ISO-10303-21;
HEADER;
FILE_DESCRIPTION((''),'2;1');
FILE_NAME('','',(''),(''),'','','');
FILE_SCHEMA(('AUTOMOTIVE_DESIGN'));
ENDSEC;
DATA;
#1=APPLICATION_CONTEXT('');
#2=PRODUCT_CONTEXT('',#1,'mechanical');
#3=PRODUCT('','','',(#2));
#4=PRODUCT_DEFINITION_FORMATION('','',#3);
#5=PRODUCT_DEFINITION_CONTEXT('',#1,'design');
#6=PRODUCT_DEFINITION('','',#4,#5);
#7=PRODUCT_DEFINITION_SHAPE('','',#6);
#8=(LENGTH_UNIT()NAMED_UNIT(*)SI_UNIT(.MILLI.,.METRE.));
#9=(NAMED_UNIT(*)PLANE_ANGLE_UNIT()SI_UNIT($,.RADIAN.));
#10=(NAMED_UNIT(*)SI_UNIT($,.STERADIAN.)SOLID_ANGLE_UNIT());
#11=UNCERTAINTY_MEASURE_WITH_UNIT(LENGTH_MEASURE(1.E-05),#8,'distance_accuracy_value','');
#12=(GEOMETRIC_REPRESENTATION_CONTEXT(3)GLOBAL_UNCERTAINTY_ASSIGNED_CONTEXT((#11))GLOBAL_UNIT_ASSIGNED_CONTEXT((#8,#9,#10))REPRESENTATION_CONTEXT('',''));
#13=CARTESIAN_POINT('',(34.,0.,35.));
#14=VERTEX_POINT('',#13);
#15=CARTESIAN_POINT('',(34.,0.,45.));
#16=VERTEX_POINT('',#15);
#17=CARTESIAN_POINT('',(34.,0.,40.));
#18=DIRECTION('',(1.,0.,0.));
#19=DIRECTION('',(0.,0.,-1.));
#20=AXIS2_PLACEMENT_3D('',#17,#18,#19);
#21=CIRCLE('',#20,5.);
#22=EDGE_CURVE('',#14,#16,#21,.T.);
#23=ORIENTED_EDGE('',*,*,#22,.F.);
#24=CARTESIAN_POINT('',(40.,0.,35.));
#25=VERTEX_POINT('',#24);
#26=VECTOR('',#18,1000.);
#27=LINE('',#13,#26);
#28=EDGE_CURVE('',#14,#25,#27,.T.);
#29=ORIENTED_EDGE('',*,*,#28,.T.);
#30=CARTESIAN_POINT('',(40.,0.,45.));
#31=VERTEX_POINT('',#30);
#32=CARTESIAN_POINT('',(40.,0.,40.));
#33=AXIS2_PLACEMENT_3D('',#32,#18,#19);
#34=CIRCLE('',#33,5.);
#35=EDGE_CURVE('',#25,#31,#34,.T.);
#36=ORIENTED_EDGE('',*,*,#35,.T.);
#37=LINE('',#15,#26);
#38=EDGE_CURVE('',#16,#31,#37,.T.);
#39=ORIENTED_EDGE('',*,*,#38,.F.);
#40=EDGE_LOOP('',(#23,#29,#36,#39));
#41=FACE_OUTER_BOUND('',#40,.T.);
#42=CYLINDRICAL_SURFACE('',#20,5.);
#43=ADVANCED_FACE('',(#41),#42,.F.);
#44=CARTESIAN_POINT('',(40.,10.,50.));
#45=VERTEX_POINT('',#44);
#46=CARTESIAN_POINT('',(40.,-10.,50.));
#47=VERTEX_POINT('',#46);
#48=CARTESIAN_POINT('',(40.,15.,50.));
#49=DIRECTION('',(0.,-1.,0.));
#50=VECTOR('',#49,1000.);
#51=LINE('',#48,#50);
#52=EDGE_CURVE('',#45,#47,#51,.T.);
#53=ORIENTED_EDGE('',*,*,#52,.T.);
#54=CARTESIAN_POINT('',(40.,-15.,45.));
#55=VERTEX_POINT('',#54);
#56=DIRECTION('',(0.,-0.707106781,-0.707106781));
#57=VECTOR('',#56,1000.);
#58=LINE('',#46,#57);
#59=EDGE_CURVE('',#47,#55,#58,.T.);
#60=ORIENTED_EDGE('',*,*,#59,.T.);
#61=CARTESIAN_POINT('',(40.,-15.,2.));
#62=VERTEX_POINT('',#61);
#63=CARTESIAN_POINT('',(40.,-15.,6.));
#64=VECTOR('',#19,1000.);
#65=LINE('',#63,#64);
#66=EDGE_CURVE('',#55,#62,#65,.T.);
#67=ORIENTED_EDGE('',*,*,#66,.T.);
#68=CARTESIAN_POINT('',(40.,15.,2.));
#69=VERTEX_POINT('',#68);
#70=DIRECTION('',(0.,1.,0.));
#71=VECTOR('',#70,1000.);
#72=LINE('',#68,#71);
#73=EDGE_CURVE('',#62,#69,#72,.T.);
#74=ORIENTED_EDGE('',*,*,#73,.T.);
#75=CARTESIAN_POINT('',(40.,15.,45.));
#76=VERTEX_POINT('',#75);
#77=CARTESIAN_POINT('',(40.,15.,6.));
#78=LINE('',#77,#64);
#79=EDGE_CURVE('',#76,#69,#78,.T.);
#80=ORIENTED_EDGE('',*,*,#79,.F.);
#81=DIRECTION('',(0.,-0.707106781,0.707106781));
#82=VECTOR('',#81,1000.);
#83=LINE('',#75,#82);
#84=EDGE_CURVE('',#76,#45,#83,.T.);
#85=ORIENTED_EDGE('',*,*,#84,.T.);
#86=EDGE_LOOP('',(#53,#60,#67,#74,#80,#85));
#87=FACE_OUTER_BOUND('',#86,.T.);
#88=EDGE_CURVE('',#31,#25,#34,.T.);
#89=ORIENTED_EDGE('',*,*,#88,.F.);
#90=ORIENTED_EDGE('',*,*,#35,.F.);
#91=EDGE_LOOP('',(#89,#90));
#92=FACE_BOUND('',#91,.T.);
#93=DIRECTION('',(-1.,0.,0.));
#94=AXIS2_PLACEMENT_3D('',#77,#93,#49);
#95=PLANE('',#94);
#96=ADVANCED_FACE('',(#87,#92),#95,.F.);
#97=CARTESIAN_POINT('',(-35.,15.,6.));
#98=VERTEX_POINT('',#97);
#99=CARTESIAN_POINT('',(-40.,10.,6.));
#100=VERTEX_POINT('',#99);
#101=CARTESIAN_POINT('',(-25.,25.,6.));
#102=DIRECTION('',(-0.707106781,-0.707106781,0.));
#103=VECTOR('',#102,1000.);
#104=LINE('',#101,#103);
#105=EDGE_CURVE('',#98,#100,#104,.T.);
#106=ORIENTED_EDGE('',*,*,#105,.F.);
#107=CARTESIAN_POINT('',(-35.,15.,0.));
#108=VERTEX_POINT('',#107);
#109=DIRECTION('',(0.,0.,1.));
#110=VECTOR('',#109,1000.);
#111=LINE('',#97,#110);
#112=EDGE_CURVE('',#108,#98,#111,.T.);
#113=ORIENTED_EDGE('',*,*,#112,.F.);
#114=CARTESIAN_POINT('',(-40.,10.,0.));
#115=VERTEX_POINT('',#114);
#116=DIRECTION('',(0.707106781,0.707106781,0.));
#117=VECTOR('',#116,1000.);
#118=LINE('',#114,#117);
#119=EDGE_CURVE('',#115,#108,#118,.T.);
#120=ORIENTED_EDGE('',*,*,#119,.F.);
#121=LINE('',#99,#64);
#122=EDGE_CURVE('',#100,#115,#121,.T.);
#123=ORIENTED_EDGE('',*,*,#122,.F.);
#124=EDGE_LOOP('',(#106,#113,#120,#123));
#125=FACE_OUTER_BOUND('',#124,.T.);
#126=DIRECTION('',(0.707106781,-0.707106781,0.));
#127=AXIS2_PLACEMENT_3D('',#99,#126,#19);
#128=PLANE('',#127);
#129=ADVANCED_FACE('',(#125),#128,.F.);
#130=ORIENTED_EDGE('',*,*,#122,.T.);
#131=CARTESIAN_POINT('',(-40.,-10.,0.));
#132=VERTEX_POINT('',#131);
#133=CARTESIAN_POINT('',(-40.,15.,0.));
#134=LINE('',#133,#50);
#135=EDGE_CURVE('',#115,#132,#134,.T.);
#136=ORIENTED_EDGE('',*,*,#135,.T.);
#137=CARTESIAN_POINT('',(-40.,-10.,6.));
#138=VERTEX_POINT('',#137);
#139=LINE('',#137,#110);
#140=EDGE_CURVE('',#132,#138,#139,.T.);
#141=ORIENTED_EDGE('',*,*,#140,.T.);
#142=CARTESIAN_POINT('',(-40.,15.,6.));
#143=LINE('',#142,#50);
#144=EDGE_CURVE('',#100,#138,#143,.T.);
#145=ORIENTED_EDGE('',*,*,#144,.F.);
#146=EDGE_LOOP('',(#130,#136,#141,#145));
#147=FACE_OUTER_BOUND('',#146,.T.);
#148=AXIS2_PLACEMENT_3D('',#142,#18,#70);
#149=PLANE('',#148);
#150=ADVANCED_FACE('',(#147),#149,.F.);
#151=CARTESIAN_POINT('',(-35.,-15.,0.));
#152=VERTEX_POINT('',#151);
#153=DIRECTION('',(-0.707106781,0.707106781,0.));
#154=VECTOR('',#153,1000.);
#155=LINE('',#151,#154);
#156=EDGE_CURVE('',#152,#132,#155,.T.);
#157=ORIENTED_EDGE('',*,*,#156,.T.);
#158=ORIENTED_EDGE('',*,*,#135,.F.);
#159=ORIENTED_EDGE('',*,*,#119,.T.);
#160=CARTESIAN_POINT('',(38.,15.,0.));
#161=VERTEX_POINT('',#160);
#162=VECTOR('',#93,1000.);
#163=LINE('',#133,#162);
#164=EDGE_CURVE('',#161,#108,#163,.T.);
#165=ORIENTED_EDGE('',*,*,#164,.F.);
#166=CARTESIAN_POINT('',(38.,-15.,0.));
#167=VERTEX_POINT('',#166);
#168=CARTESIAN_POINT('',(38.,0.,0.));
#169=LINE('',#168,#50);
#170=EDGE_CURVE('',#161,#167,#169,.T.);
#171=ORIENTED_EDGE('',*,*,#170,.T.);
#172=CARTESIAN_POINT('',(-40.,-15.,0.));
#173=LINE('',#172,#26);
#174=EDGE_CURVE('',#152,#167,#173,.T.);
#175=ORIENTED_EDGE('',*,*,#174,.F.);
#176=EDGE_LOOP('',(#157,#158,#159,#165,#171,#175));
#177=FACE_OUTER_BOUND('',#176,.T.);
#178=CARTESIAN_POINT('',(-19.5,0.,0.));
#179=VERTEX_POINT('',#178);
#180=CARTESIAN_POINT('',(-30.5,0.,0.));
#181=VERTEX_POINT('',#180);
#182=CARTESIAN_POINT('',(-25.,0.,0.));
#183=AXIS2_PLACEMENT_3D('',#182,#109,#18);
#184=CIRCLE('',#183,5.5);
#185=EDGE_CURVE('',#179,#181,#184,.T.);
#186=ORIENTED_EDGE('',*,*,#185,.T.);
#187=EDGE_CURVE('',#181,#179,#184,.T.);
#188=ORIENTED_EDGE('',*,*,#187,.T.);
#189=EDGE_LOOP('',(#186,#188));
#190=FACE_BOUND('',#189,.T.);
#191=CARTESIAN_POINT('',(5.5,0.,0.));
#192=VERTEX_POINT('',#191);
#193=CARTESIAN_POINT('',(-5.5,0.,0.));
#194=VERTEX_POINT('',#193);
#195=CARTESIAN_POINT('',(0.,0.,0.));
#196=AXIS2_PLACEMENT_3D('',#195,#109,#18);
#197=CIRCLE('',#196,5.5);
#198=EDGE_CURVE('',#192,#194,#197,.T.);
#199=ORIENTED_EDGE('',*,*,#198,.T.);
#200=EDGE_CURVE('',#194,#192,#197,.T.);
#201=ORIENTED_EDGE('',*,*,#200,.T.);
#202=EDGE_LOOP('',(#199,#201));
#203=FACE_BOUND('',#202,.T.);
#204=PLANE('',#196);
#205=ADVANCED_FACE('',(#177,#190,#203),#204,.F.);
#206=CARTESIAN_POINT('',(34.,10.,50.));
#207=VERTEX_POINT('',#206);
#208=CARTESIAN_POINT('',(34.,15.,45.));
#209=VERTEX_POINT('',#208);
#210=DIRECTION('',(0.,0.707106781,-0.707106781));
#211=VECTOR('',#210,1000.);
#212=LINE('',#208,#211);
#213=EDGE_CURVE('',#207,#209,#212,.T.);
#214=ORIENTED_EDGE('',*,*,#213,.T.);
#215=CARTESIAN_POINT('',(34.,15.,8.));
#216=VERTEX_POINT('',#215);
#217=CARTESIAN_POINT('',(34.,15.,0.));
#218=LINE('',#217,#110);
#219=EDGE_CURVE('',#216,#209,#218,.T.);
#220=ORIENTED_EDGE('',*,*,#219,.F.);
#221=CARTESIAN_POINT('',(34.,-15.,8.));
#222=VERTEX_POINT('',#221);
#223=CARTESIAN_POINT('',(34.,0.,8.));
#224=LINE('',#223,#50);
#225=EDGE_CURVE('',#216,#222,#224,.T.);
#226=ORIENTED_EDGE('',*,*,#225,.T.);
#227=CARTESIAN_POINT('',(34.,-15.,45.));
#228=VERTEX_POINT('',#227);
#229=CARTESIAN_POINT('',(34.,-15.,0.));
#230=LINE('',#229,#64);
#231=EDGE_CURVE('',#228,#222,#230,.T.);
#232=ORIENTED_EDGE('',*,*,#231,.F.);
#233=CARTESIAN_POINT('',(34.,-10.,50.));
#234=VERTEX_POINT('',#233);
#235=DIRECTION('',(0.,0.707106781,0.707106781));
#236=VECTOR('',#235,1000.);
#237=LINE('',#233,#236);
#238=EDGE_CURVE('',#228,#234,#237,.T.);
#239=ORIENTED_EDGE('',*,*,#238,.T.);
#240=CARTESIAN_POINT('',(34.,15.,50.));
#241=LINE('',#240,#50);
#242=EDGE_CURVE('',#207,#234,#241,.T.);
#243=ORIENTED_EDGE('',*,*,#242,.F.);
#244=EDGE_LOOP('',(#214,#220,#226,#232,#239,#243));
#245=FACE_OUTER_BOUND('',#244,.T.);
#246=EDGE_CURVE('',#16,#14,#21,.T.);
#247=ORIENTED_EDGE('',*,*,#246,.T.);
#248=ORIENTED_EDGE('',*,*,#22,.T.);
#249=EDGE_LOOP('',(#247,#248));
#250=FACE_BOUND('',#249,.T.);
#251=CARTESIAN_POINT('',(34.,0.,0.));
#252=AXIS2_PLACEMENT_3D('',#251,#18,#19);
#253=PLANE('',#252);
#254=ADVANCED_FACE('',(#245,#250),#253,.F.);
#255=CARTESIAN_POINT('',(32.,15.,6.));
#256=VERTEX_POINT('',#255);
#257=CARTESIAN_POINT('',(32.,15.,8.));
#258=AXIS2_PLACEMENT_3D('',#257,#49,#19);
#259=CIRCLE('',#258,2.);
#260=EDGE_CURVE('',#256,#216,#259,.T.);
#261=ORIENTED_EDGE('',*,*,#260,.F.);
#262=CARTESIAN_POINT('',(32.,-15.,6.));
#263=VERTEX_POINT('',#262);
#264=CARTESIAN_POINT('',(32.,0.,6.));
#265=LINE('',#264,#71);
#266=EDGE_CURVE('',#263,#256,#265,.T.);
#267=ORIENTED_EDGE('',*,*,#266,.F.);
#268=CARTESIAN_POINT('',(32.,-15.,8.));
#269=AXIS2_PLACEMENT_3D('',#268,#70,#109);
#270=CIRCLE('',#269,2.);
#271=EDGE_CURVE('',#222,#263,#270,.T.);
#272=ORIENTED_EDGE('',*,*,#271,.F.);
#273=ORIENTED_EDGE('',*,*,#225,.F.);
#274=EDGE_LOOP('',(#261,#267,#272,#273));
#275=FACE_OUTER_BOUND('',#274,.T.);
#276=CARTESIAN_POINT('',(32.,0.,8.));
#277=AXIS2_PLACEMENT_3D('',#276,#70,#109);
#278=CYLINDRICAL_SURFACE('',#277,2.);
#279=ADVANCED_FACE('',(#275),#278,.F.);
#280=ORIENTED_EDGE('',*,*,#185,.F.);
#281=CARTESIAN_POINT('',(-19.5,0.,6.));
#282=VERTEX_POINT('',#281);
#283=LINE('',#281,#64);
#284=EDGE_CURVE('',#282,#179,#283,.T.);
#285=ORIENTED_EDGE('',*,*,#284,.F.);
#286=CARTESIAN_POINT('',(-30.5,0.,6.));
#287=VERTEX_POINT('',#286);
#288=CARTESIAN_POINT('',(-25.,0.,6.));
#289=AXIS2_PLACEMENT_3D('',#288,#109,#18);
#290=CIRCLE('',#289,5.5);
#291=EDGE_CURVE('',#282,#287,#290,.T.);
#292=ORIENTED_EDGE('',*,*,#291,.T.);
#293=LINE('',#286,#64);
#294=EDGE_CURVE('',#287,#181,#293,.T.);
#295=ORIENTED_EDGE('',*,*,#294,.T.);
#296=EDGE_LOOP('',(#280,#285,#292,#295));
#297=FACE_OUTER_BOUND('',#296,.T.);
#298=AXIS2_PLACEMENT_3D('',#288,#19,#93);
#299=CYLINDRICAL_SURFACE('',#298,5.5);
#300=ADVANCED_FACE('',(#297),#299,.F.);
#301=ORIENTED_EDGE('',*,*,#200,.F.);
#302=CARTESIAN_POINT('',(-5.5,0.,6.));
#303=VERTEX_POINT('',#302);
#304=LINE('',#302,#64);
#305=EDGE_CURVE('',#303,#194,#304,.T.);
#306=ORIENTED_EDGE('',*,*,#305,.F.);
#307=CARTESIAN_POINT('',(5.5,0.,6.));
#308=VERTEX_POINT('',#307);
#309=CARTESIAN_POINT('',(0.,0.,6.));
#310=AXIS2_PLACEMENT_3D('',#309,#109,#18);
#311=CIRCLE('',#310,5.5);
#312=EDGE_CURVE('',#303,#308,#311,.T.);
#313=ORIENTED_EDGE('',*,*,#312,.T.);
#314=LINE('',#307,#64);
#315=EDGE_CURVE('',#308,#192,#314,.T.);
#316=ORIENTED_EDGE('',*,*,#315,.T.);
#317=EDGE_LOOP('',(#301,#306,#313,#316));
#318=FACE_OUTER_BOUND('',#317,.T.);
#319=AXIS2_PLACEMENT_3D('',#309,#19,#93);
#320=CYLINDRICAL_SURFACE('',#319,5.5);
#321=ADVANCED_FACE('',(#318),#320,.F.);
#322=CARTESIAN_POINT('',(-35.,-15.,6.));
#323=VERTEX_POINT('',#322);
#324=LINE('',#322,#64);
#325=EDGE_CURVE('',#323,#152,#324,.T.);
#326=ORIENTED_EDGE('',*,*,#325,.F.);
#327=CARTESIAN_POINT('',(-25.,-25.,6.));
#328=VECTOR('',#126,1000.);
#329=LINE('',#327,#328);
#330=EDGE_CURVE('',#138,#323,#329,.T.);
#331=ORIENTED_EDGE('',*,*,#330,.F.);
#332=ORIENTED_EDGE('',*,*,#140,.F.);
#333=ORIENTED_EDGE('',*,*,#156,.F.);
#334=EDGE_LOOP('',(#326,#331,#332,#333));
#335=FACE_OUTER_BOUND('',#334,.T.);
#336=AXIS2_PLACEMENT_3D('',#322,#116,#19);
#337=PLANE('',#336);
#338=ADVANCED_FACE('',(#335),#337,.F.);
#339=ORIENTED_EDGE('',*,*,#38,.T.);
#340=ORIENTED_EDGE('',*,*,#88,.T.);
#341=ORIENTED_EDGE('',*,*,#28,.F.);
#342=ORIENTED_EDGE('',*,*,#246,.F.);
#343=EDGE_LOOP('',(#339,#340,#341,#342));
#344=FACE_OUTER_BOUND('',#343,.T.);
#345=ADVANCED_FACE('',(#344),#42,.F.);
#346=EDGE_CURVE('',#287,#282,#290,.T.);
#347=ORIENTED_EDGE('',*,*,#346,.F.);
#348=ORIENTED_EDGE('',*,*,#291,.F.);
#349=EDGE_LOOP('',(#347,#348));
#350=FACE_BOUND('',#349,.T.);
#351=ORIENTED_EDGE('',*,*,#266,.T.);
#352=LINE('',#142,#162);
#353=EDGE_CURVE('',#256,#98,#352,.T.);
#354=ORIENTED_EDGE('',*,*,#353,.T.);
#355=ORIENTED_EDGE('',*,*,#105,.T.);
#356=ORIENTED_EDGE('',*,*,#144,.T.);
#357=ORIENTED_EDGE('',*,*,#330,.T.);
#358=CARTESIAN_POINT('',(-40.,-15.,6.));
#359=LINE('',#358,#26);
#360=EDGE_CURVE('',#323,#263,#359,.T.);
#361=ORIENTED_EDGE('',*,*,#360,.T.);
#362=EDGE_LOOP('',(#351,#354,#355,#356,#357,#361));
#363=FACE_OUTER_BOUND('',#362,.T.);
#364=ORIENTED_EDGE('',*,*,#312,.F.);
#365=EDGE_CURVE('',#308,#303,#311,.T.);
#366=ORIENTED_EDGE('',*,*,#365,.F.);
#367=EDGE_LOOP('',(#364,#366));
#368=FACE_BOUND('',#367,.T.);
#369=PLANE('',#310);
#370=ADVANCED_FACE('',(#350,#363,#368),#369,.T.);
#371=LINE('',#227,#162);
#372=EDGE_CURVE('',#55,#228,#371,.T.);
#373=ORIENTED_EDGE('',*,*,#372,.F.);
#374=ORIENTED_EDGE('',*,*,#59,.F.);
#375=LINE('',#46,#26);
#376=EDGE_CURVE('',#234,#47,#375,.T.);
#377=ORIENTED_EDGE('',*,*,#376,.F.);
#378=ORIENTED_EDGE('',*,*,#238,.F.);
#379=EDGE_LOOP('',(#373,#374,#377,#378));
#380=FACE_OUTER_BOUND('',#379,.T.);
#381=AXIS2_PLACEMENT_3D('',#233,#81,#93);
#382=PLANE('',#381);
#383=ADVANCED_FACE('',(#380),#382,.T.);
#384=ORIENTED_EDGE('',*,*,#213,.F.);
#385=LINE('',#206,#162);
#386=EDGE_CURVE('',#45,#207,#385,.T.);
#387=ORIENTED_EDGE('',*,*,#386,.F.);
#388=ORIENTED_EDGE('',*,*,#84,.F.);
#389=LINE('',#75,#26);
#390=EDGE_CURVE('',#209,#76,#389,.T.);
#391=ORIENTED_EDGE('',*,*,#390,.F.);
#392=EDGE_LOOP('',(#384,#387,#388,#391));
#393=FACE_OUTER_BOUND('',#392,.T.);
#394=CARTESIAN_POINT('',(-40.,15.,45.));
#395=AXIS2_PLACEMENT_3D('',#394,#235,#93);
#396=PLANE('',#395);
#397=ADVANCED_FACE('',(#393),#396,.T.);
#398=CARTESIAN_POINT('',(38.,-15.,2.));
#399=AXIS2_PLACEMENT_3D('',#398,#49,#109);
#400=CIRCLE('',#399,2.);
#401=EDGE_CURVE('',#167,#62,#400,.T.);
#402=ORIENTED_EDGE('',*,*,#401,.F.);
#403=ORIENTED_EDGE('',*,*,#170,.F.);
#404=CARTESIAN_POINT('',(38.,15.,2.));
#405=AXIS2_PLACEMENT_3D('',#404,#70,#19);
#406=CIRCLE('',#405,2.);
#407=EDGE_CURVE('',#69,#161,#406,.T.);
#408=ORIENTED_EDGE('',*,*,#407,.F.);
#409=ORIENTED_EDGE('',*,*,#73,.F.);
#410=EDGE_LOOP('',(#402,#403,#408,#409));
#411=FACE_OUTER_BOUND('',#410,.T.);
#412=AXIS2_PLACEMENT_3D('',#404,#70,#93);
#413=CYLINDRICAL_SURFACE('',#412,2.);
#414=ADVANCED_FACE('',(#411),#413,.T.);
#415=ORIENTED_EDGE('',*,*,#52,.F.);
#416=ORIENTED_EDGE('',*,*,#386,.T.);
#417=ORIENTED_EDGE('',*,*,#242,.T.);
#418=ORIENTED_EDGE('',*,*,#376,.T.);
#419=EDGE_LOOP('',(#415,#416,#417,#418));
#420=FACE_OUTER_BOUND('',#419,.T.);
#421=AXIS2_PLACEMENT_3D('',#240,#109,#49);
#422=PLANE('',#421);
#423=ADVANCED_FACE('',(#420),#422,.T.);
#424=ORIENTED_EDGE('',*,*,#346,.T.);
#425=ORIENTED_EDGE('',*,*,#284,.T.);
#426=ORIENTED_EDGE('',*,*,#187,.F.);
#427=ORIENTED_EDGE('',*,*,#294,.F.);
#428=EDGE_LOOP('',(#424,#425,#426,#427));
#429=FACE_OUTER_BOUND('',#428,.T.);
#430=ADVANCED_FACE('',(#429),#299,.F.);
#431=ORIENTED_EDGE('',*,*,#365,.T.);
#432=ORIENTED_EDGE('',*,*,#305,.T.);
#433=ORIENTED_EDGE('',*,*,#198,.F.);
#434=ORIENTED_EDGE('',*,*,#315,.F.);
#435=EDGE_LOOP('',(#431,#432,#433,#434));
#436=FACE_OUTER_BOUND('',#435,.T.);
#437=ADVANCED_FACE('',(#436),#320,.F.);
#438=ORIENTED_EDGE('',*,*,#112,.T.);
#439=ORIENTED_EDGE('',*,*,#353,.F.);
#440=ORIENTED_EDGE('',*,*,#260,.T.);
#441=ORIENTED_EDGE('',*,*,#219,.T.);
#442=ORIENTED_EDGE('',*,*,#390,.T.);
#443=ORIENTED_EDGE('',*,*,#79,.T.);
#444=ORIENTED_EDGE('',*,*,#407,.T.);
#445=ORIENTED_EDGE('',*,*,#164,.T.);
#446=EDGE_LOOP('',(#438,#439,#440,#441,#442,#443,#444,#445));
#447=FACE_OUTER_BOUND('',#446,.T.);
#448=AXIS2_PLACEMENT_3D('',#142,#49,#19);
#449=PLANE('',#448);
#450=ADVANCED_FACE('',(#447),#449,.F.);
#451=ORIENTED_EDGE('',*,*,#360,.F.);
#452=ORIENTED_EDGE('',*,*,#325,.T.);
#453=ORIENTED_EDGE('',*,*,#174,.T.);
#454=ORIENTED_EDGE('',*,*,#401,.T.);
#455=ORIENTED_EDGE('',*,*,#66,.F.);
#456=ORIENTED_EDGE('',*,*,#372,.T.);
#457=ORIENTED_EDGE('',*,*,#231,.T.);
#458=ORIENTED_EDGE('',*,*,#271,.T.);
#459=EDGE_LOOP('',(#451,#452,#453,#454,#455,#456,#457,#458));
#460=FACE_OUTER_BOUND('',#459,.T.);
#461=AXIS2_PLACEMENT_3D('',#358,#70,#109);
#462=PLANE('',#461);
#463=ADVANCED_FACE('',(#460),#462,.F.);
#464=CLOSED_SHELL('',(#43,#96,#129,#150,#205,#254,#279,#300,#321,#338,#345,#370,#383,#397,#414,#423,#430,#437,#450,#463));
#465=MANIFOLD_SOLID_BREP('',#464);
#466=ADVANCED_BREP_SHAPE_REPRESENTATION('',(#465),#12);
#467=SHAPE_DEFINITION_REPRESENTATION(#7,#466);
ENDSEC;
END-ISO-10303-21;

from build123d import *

# Parameters (mm, degrees)
SKETCH1_W           = 80
SKETCH1_H           = 30
SKETCH1_R           = 5.5
BOSS_EXTRUDE1_DEPTH = 6
SKETCH3_W           = 50
SKETCH3_H           = 30
SKETCH3_R           = 5
BOSS_EXTRUDE2_DEPTH = 6
FILLET1_R           = 2
CHAMFER1_SIZE       = 5


with BuildPart() as part:
    # Sketch1 → Boss-Extrude1 (new body)
    with BuildSketch(Plane.XY):
        Rectangle(SKETCH1_W, SKETCH1_H)
        Circle(SKETCH1_R, mode=Mode.SUBTRACT)
        with Locations((-25, 0)):
            Circle(SKETCH1_R, mode=Mode.SUBTRACT)
    extrude(amount=BOSS_EXTRUDE1_DEPTH)

    # Sketch3 → Boss-Extrude2 (add)
    with BuildSketch(Plane(origin=(40, 0, 0), x_dir=(0, 0, -1), z_dir=(1, 0, 0))):
        with Locations((-25, 0)):
            Rectangle(SKETCH3_W, SKETCH3_H)
        with Locations((-40, 0)):
            Circle(SKETCH3_R, mode=Mode.SUBTRACT)
    extrude(amount=-BOSS_EXTRUDE2_DEPTH)

    # Fillet1
    fillet1_edges = [part.edges().sort_by_distance(p)[0] for p in [
        (34, 0, 6),
        (40, 0, 0),
    ]]
    fillet(fillet1_edges, radius=FILLET1_R)

    # Chamfer1
    chamfer1_edges = [part.edges().sort_by_distance(p)[0] for p in [
        (37, 15, 50),
        (37, -15, 50),
        (-40, -15, 3),
        (-40, 15, 3),
    ]]
    chamfer(chamfer1_edges, length=CHAMFER1_SIZE)


solid = part.part
